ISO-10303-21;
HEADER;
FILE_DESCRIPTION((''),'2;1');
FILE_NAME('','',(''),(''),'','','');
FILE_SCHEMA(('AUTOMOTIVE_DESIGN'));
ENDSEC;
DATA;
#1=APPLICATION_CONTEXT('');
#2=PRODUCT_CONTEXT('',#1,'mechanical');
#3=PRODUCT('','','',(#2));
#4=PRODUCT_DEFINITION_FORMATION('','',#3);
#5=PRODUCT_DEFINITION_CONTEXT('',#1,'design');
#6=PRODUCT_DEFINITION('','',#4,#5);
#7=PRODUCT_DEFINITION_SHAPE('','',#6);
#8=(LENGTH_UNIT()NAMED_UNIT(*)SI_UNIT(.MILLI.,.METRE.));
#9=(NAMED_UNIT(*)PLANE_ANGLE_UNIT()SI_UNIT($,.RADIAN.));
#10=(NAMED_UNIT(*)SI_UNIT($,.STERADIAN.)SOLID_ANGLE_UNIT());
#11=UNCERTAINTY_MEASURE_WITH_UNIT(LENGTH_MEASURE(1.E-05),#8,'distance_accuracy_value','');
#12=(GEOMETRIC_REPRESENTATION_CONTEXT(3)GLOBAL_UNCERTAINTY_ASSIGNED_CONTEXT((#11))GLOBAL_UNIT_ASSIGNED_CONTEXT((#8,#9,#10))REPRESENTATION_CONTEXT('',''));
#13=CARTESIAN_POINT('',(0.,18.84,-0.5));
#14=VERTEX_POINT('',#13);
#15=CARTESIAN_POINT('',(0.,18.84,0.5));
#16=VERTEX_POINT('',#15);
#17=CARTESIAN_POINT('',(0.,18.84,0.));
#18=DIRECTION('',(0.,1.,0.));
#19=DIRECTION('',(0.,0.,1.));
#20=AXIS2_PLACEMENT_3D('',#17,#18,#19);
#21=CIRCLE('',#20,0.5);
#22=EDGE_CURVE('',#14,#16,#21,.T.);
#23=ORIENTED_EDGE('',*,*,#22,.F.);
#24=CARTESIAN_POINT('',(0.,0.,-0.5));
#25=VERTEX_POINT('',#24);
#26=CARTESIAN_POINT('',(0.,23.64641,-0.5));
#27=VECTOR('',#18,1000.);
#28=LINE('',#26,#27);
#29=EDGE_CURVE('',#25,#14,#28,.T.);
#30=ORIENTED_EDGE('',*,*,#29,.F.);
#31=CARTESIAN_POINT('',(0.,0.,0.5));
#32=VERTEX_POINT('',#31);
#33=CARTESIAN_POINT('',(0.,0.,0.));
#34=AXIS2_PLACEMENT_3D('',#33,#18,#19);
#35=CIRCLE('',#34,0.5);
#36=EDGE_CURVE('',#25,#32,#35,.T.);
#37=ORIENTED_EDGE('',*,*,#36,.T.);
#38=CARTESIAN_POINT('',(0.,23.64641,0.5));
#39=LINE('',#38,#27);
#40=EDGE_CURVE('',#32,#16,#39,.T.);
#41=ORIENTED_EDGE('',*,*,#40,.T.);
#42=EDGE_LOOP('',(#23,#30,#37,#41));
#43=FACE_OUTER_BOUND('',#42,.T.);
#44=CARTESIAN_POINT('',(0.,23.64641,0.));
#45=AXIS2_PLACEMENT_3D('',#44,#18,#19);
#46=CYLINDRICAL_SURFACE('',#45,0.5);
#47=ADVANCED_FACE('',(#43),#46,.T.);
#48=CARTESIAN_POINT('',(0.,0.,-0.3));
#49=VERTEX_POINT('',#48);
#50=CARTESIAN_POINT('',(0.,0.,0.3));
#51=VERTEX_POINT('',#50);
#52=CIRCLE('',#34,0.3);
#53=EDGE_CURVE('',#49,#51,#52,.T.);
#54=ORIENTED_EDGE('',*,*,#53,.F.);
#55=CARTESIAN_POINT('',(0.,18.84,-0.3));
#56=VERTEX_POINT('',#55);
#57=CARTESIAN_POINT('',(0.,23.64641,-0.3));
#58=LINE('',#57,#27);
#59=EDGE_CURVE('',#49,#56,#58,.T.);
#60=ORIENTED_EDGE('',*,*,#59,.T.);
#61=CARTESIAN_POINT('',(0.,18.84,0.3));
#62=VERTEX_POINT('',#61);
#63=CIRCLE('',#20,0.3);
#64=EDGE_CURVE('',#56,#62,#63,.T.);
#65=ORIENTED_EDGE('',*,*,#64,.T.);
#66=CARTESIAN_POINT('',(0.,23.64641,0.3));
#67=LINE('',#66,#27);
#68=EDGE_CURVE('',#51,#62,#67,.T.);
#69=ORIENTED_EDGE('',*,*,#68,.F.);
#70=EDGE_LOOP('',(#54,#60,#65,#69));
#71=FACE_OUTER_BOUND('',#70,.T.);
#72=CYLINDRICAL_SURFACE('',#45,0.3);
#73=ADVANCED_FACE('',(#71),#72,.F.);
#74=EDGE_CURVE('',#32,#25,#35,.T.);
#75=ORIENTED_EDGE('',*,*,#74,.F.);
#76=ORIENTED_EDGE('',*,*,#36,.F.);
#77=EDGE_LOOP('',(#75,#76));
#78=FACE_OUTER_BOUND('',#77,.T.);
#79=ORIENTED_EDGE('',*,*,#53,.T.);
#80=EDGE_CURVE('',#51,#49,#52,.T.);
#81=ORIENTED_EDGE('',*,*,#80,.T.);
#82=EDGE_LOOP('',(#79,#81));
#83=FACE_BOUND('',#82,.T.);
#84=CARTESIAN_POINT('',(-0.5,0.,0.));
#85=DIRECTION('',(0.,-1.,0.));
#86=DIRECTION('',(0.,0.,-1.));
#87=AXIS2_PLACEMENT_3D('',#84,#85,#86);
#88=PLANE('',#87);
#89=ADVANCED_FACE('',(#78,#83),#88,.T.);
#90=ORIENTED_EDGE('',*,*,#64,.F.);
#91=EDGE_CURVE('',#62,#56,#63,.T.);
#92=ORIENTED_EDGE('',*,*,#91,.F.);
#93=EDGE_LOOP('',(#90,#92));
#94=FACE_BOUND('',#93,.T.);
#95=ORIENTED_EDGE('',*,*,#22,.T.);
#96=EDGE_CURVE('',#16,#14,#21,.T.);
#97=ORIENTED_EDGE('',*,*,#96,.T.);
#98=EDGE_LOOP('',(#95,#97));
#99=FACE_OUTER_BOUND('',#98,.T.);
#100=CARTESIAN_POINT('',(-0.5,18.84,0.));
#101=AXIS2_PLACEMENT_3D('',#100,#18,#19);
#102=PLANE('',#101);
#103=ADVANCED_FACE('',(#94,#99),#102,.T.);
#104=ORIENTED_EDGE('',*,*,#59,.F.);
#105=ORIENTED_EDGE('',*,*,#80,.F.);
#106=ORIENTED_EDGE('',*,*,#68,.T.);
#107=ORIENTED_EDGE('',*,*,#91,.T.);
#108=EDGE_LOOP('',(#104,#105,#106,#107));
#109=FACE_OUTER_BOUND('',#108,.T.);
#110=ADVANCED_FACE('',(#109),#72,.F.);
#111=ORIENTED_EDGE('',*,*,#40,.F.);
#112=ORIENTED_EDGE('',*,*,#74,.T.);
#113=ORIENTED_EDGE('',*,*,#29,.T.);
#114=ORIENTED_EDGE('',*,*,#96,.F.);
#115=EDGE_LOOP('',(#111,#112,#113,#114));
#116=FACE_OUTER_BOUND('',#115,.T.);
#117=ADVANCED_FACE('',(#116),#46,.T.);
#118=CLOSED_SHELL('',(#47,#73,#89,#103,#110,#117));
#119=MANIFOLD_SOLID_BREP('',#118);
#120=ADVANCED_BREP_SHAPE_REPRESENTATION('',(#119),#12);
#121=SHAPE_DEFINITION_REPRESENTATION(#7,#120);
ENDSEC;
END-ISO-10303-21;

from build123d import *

# Parameters (mm, degrees)
SKETCH1_W = 0.2
SKETCH1_H = 18.84


with BuildPart() as part:
    # Sketch1 → Revolve2 (revolve)
    with BuildSketch(Plane.XY, mode=Mode.PRIVATE) as revolve2_sk:
        with Locations((-0.4, 9.42)):
            Rectangle(SKETCH1_W, SKETCH1_H)
    revolve(revolve2_sk.sketch.rotate(Axis((0, 23.646410138, 0), (0, -1, 0)), 270), axis=Axis((0, 23.646410138, 0), (0, -1, 0)))


solid = part.part
